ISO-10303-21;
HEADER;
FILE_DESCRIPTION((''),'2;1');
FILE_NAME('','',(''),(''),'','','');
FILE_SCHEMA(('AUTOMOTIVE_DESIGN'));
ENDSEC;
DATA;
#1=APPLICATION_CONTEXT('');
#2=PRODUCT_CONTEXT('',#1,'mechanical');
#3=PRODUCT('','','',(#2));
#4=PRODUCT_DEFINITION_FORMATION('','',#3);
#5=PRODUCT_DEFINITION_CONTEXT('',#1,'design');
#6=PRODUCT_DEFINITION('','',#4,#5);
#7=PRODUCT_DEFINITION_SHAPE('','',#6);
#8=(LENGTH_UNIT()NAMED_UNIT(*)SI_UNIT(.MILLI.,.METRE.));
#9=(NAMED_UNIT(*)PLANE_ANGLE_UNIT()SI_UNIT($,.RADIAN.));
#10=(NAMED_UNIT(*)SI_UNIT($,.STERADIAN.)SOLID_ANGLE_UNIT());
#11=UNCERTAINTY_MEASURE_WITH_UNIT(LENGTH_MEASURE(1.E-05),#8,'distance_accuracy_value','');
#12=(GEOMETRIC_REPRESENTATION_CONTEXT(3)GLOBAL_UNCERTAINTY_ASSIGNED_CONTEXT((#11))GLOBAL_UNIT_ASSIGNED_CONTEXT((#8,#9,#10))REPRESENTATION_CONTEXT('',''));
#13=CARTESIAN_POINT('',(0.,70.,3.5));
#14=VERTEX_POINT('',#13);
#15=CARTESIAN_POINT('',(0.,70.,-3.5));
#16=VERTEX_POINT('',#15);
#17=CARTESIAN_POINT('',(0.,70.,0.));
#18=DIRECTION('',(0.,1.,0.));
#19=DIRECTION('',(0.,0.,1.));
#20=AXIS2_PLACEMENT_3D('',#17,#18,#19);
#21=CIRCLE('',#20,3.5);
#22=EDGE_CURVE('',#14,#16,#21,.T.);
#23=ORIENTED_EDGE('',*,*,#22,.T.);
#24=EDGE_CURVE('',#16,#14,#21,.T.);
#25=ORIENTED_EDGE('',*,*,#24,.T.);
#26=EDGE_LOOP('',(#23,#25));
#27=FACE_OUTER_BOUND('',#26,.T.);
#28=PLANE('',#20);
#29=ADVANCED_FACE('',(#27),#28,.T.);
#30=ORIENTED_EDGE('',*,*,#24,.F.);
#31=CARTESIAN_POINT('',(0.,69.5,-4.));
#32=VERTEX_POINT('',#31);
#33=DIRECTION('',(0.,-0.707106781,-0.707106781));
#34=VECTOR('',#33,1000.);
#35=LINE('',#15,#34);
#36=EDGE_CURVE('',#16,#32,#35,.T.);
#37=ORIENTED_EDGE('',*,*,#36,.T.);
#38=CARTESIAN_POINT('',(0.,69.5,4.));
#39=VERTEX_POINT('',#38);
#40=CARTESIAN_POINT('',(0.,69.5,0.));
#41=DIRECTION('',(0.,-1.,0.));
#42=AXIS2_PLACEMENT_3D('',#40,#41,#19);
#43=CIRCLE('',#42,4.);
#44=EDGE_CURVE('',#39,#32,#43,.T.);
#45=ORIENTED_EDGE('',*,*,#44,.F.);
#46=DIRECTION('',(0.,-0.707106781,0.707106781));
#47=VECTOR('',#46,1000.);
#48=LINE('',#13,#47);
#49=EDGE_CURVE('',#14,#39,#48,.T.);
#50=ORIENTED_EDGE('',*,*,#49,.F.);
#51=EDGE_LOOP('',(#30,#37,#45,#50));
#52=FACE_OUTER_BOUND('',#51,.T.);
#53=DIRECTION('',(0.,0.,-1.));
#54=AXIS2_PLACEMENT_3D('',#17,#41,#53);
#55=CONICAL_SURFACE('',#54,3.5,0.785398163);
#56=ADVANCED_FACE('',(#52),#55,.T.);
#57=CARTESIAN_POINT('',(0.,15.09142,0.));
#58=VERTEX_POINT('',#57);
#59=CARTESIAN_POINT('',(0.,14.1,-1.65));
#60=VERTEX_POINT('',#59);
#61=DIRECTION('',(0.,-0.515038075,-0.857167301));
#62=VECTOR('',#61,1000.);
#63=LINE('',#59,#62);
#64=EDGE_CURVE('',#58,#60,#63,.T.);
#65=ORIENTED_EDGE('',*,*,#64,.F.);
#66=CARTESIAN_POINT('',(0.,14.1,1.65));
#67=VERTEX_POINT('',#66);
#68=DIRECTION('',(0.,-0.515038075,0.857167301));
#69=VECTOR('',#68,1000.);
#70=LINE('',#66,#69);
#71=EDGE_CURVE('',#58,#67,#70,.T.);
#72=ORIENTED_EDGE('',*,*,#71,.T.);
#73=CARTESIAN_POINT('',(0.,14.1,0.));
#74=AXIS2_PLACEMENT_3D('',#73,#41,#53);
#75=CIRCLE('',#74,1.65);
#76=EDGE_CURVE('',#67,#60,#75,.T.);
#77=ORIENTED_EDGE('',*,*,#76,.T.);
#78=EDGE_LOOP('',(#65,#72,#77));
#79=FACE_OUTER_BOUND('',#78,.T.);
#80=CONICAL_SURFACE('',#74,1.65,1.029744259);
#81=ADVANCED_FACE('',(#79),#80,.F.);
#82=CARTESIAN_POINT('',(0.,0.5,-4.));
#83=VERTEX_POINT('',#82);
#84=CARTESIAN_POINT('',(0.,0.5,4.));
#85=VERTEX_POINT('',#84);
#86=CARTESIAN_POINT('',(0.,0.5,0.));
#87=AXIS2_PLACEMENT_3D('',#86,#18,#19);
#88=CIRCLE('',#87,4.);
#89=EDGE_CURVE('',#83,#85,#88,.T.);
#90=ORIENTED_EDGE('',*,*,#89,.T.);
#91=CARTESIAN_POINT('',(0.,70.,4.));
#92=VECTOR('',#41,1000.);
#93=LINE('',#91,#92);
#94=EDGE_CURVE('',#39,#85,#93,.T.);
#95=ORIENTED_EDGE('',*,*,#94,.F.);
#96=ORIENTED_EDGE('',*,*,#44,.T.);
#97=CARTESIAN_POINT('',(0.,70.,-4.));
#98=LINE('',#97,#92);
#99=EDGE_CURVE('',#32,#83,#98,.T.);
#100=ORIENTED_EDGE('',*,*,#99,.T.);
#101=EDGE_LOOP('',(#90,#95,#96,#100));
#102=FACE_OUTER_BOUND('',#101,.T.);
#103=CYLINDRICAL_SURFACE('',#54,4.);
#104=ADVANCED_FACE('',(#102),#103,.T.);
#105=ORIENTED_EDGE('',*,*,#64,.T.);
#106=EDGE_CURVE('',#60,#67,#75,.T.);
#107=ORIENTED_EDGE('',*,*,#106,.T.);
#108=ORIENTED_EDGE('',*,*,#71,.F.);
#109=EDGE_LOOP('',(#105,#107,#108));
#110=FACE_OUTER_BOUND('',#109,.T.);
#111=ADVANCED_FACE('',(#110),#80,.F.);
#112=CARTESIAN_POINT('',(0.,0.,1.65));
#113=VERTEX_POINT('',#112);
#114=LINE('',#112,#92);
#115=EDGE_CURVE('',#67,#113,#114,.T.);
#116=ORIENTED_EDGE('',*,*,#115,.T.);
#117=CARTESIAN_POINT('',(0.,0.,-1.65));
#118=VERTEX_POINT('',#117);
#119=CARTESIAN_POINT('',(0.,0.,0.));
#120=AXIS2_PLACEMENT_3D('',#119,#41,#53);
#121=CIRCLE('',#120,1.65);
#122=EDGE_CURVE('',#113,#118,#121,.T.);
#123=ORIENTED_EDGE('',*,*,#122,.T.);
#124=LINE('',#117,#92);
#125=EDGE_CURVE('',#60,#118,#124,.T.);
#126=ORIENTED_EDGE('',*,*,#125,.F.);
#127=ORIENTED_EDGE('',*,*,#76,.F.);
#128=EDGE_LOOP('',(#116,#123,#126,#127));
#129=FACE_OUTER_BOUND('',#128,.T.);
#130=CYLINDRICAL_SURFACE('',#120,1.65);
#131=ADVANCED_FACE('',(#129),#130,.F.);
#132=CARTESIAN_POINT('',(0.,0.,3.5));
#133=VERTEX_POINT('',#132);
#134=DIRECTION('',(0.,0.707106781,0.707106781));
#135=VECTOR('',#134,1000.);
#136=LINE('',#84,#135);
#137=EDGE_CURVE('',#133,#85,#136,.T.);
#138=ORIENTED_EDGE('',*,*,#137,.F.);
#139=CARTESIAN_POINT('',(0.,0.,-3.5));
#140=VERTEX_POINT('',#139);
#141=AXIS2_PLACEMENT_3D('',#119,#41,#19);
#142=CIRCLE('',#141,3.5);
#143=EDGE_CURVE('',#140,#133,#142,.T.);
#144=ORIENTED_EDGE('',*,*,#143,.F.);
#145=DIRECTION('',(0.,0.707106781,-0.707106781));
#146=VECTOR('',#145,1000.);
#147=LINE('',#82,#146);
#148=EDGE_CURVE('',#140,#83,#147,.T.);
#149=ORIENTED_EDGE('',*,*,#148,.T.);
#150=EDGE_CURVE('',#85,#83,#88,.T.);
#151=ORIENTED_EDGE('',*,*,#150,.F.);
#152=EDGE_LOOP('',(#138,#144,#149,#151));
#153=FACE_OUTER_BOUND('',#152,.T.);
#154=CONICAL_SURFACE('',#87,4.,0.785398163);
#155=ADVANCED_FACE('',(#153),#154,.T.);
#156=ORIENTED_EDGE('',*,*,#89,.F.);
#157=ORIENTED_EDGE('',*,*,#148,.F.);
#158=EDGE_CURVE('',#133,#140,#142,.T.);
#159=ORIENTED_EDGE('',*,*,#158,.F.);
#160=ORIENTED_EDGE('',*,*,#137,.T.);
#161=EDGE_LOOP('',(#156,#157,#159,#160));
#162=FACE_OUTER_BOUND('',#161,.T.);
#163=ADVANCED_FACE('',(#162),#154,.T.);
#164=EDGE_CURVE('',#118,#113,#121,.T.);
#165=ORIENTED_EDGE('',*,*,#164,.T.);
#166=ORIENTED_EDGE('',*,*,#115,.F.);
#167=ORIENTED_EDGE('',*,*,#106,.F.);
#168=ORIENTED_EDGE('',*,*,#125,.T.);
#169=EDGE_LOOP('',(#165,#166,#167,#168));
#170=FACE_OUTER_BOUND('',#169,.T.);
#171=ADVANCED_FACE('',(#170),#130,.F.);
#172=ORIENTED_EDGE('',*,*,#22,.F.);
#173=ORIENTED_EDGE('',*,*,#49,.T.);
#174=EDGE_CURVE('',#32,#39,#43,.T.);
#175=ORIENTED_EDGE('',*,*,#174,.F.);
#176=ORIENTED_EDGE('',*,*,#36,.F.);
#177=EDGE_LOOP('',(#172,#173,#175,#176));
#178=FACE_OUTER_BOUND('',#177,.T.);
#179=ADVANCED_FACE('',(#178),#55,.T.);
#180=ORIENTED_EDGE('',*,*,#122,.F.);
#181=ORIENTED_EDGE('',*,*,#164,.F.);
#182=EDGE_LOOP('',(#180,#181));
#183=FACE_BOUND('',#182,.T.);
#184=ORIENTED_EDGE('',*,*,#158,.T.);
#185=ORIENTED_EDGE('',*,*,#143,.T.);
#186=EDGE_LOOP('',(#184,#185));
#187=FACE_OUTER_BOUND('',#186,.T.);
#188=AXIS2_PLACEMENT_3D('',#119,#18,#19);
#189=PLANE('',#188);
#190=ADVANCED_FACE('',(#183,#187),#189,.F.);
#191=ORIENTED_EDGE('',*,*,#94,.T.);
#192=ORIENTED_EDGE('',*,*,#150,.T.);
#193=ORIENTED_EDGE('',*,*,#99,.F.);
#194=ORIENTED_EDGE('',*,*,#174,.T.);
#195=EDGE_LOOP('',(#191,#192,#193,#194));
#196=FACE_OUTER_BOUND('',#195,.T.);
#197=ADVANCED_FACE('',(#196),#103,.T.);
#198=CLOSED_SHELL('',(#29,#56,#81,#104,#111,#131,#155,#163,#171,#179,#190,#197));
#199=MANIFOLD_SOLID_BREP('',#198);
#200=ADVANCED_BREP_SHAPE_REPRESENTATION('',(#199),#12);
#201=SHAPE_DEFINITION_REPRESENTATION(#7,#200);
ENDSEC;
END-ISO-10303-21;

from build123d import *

# Parameters (mm, degrees)
SKETCH_1_R             = 4
EXTRUDE_1_DEPTH        = 70
CHAMFER_1_SIZE         = 0.5
HOLE_WIZARD_M4_1_D     = 3.3
HOLE_WIZARD_M4_1_DEPTH = 14.1
HOLE_WIZARD_M4_1_TIP   = 0.991420021


with BuildPart() as part:
    # 草图1 → 凸台-拉伸1 (new body)
    with BuildSketch(Plane(origin=(0, 0, 0), x_dir=(1, 0, 0), z_dir=(0, 1, 0))):
        with Locations(Location((0, 0, 0), (0, 0, 270))):
            Circle(SKETCH_1_R)
    extrude(amount=EXTRUDE_1_DEPTH)

    # 倒角1
    chamfer_1_edges = [part.edges().sort_by_distance(p)[0] for p in [
        (0, 0, -4),
        (0, 70, -4),
    ]]
    chamfer(chamfer_1_edges, length=CHAMFER_1_SIZE)

    # M4 螺纹孔1
    with Locations(Plane(origin=(0, 0, 0), x_dir=(-1, 0, 0), z_dir=(0, -1, 0))):
        with Locations((0, 0)):
            Hole(HOLE_WIZARD_M4_1_D / 2, depth=HOLE_WIZARD_M4_1_DEPTH)
            with Locations((0, 0, -(HOLE_WIZARD_M4_1_DEPTH + HOLE_WIZARD_M4_1_TIP / 2))):  # 118° drill point
                Cone(0, HOLE_WIZARD_M4_1_D / 2, HOLE_WIZARD_M4_1_TIP, mode=Mode.SUBTRACT)


solid = part.part
